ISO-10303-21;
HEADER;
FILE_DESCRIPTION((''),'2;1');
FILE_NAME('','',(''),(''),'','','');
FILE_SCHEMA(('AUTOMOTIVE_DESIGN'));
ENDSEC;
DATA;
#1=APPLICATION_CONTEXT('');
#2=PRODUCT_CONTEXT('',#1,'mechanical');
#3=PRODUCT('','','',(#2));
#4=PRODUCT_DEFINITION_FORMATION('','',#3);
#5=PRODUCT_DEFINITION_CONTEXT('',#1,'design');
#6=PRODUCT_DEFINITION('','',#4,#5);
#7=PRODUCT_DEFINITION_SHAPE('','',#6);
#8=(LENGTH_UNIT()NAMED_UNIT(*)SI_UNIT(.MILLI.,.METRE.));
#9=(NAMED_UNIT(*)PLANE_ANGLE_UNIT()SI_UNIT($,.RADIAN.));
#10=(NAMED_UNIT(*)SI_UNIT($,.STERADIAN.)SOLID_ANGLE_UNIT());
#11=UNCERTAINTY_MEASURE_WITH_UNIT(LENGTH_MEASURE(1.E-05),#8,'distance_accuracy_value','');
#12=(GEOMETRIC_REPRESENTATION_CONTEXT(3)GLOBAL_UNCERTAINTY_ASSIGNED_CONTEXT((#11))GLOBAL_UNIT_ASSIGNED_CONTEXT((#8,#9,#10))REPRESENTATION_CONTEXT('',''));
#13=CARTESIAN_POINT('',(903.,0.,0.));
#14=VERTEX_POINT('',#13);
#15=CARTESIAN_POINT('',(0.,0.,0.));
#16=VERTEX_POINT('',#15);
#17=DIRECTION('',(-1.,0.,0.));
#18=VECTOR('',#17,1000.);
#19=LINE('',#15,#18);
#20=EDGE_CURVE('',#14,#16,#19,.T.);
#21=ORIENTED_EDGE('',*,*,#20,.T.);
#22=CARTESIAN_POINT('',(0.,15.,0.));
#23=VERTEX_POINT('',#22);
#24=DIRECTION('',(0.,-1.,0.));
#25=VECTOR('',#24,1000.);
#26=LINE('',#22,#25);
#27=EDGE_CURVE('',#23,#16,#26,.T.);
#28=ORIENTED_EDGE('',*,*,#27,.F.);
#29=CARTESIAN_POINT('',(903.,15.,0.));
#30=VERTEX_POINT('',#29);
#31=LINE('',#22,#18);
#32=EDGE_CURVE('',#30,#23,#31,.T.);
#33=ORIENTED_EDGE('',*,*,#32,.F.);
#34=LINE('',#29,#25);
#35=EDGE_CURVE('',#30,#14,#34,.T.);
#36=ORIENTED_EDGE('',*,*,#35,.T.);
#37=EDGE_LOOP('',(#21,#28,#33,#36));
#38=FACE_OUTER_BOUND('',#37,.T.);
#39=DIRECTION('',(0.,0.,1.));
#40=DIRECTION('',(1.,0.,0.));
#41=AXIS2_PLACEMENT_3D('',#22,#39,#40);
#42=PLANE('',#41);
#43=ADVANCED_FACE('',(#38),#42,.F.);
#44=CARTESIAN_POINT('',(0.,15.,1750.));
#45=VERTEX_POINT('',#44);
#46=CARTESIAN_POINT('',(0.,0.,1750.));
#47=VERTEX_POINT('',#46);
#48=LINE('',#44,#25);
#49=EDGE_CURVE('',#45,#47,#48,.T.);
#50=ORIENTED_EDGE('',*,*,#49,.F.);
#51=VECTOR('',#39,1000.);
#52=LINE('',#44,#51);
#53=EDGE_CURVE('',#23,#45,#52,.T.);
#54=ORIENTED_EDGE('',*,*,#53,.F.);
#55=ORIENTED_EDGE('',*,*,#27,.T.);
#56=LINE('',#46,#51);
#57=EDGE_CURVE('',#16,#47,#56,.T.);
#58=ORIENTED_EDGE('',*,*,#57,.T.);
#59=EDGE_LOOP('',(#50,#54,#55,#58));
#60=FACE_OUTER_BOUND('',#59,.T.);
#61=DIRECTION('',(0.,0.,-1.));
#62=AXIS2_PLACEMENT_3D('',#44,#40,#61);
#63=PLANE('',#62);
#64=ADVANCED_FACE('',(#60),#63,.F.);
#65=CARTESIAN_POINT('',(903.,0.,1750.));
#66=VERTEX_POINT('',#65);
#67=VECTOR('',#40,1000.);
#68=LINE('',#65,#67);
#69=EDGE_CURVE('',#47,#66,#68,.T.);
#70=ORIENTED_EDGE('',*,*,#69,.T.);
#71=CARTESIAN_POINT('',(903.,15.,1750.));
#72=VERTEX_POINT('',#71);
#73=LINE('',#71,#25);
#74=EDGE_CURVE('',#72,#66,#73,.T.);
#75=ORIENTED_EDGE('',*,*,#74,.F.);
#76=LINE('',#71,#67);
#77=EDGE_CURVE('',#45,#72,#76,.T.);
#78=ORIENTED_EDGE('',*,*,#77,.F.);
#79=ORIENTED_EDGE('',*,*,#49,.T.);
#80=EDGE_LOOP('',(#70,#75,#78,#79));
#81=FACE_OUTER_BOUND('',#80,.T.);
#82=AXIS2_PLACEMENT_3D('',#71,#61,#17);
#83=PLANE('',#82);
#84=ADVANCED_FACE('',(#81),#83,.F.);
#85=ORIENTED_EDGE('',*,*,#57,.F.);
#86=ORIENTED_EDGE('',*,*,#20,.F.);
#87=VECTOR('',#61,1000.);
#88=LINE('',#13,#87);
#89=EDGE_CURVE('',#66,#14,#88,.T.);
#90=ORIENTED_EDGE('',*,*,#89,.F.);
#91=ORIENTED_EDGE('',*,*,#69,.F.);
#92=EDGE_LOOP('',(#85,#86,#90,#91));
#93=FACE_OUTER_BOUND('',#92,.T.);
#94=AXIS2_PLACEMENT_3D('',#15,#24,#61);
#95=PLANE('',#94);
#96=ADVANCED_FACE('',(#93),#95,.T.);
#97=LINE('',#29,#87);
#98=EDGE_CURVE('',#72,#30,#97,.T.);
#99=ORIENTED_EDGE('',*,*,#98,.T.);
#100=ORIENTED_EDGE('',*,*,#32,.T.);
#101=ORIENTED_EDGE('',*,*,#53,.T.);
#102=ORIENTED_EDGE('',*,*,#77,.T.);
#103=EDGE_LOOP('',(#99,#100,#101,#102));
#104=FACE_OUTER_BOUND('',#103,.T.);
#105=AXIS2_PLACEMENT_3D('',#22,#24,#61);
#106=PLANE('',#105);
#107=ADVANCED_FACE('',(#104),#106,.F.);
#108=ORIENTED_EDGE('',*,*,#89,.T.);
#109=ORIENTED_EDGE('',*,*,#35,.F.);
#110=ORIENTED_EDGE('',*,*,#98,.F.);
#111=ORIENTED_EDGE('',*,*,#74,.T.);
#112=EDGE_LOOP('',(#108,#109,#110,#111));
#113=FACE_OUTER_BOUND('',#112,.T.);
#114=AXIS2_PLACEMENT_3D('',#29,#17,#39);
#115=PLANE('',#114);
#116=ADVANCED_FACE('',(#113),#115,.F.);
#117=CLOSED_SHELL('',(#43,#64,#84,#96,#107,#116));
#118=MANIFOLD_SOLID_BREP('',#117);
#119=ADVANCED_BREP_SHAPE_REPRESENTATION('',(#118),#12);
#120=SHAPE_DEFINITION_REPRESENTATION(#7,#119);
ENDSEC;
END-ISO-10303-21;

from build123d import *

# Parameters (mm, degrees)
SKETCH_1_W      = 903
SKETCH_1_H      = 1750
EXTRUDE_1_DEPTH = 15


with BuildPart() as part:
    # 草图1 → 凸台-拉伸1 (new body)
    with BuildSketch(Plane(origin=(0, 0, 0), x_dir=(1, 0, 0), z_dir=(0, 1, 0))):
        with Locations((451.5, -875)):
            Rectangle(SKETCH_1_W, SKETCH_1_H)
    extrude(amount=EXTRUDE_1_DEPTH)


solid = part.part
